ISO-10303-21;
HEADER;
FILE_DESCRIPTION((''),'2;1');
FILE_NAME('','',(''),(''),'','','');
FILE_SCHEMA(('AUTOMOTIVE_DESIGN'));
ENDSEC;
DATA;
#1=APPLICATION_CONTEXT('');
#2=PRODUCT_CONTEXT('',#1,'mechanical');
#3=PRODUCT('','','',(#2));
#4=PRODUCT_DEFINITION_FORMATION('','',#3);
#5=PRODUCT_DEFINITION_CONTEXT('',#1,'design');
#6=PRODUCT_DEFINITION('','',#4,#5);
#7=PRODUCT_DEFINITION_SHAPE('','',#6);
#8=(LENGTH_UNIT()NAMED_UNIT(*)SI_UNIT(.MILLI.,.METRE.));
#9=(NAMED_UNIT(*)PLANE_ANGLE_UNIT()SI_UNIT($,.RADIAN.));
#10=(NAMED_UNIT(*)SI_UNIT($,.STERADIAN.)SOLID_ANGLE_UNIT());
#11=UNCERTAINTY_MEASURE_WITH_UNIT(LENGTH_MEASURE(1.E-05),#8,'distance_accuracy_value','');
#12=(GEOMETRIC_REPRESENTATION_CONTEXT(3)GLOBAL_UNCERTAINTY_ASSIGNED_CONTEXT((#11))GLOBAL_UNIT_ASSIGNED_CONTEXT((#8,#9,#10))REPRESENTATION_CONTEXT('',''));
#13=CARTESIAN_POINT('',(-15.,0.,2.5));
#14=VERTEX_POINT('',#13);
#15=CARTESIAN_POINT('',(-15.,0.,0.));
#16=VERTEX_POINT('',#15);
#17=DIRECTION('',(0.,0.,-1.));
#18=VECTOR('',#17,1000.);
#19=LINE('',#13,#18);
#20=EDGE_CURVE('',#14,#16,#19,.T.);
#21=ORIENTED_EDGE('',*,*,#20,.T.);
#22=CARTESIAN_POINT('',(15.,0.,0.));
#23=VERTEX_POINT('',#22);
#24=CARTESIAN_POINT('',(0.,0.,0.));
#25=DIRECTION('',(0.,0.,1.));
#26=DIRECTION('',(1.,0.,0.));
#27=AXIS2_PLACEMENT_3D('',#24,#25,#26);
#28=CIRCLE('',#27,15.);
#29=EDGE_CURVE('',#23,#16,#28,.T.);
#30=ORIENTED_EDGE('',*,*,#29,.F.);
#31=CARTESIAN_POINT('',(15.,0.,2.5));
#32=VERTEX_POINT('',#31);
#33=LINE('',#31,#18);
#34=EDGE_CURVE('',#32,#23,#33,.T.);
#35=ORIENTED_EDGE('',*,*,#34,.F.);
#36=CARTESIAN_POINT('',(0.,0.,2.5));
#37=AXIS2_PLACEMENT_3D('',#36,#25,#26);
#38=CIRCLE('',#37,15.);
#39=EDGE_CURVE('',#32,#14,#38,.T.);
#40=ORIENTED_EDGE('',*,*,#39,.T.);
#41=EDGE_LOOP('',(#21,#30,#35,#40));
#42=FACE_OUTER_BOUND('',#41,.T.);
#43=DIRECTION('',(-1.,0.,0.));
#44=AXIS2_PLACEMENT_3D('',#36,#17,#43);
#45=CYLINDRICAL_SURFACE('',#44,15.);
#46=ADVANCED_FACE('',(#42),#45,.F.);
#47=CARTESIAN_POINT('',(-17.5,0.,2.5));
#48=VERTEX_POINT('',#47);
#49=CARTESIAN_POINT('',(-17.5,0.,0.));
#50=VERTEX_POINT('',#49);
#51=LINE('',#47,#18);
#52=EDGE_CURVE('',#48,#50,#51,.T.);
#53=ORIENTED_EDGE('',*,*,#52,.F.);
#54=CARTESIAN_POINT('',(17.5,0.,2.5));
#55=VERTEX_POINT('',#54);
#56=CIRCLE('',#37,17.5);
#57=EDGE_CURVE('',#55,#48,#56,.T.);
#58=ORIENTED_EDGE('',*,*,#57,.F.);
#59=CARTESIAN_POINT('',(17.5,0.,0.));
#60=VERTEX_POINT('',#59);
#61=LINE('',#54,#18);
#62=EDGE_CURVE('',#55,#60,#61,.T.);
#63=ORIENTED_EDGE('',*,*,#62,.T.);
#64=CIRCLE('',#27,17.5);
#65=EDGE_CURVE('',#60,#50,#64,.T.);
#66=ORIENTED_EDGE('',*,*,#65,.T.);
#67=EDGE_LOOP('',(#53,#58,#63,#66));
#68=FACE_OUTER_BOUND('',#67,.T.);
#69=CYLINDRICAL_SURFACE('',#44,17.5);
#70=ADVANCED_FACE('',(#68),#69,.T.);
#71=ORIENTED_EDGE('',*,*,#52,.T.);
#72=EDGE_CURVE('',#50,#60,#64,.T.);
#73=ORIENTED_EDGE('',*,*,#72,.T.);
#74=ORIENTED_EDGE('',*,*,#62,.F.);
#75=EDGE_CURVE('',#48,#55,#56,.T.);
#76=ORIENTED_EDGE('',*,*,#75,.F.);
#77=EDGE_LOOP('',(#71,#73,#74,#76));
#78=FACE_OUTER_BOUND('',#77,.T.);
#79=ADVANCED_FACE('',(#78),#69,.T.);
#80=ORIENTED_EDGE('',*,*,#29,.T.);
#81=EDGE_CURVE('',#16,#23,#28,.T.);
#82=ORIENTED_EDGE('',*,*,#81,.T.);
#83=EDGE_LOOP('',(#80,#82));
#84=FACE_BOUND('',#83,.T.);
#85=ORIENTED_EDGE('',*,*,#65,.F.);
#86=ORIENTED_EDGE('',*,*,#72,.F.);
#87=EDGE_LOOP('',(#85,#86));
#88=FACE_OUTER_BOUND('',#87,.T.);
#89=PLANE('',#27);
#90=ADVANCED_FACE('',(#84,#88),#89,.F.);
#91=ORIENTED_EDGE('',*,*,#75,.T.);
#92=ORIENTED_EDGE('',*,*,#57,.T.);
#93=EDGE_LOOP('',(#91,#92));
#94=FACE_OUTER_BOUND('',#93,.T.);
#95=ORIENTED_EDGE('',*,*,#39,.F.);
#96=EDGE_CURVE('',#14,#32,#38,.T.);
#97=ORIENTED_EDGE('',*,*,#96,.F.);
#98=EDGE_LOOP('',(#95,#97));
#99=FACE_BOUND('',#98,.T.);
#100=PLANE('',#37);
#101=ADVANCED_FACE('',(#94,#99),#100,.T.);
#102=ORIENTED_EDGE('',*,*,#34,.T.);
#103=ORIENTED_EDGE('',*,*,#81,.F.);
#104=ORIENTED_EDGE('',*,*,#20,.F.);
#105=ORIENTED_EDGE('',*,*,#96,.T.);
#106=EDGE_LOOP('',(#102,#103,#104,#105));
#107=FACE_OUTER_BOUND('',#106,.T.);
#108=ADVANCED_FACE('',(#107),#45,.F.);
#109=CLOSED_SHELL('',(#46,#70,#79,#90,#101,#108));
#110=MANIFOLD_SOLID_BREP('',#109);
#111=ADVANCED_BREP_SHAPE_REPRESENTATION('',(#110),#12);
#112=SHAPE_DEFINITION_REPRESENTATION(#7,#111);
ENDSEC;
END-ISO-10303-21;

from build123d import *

# Parameters (mm, degrees)
SKETCH_1_R      = 17.5
SKETCH_1_R_2    = 15
EXTRUDE_1_DEPTH = 2.5


with BuildPart() as part:
    # 草图1 → 凸台-拉伸1 (new body)
    with BuildSketch(Plane.XY):
        Circle(SKETCH_1_R)
        Circle(SKETCH_1_R_2, mode=Mode.SUBTRACT)
    extrude(amount=EXTRUDE_1_DEPTH)


solid = part.part
